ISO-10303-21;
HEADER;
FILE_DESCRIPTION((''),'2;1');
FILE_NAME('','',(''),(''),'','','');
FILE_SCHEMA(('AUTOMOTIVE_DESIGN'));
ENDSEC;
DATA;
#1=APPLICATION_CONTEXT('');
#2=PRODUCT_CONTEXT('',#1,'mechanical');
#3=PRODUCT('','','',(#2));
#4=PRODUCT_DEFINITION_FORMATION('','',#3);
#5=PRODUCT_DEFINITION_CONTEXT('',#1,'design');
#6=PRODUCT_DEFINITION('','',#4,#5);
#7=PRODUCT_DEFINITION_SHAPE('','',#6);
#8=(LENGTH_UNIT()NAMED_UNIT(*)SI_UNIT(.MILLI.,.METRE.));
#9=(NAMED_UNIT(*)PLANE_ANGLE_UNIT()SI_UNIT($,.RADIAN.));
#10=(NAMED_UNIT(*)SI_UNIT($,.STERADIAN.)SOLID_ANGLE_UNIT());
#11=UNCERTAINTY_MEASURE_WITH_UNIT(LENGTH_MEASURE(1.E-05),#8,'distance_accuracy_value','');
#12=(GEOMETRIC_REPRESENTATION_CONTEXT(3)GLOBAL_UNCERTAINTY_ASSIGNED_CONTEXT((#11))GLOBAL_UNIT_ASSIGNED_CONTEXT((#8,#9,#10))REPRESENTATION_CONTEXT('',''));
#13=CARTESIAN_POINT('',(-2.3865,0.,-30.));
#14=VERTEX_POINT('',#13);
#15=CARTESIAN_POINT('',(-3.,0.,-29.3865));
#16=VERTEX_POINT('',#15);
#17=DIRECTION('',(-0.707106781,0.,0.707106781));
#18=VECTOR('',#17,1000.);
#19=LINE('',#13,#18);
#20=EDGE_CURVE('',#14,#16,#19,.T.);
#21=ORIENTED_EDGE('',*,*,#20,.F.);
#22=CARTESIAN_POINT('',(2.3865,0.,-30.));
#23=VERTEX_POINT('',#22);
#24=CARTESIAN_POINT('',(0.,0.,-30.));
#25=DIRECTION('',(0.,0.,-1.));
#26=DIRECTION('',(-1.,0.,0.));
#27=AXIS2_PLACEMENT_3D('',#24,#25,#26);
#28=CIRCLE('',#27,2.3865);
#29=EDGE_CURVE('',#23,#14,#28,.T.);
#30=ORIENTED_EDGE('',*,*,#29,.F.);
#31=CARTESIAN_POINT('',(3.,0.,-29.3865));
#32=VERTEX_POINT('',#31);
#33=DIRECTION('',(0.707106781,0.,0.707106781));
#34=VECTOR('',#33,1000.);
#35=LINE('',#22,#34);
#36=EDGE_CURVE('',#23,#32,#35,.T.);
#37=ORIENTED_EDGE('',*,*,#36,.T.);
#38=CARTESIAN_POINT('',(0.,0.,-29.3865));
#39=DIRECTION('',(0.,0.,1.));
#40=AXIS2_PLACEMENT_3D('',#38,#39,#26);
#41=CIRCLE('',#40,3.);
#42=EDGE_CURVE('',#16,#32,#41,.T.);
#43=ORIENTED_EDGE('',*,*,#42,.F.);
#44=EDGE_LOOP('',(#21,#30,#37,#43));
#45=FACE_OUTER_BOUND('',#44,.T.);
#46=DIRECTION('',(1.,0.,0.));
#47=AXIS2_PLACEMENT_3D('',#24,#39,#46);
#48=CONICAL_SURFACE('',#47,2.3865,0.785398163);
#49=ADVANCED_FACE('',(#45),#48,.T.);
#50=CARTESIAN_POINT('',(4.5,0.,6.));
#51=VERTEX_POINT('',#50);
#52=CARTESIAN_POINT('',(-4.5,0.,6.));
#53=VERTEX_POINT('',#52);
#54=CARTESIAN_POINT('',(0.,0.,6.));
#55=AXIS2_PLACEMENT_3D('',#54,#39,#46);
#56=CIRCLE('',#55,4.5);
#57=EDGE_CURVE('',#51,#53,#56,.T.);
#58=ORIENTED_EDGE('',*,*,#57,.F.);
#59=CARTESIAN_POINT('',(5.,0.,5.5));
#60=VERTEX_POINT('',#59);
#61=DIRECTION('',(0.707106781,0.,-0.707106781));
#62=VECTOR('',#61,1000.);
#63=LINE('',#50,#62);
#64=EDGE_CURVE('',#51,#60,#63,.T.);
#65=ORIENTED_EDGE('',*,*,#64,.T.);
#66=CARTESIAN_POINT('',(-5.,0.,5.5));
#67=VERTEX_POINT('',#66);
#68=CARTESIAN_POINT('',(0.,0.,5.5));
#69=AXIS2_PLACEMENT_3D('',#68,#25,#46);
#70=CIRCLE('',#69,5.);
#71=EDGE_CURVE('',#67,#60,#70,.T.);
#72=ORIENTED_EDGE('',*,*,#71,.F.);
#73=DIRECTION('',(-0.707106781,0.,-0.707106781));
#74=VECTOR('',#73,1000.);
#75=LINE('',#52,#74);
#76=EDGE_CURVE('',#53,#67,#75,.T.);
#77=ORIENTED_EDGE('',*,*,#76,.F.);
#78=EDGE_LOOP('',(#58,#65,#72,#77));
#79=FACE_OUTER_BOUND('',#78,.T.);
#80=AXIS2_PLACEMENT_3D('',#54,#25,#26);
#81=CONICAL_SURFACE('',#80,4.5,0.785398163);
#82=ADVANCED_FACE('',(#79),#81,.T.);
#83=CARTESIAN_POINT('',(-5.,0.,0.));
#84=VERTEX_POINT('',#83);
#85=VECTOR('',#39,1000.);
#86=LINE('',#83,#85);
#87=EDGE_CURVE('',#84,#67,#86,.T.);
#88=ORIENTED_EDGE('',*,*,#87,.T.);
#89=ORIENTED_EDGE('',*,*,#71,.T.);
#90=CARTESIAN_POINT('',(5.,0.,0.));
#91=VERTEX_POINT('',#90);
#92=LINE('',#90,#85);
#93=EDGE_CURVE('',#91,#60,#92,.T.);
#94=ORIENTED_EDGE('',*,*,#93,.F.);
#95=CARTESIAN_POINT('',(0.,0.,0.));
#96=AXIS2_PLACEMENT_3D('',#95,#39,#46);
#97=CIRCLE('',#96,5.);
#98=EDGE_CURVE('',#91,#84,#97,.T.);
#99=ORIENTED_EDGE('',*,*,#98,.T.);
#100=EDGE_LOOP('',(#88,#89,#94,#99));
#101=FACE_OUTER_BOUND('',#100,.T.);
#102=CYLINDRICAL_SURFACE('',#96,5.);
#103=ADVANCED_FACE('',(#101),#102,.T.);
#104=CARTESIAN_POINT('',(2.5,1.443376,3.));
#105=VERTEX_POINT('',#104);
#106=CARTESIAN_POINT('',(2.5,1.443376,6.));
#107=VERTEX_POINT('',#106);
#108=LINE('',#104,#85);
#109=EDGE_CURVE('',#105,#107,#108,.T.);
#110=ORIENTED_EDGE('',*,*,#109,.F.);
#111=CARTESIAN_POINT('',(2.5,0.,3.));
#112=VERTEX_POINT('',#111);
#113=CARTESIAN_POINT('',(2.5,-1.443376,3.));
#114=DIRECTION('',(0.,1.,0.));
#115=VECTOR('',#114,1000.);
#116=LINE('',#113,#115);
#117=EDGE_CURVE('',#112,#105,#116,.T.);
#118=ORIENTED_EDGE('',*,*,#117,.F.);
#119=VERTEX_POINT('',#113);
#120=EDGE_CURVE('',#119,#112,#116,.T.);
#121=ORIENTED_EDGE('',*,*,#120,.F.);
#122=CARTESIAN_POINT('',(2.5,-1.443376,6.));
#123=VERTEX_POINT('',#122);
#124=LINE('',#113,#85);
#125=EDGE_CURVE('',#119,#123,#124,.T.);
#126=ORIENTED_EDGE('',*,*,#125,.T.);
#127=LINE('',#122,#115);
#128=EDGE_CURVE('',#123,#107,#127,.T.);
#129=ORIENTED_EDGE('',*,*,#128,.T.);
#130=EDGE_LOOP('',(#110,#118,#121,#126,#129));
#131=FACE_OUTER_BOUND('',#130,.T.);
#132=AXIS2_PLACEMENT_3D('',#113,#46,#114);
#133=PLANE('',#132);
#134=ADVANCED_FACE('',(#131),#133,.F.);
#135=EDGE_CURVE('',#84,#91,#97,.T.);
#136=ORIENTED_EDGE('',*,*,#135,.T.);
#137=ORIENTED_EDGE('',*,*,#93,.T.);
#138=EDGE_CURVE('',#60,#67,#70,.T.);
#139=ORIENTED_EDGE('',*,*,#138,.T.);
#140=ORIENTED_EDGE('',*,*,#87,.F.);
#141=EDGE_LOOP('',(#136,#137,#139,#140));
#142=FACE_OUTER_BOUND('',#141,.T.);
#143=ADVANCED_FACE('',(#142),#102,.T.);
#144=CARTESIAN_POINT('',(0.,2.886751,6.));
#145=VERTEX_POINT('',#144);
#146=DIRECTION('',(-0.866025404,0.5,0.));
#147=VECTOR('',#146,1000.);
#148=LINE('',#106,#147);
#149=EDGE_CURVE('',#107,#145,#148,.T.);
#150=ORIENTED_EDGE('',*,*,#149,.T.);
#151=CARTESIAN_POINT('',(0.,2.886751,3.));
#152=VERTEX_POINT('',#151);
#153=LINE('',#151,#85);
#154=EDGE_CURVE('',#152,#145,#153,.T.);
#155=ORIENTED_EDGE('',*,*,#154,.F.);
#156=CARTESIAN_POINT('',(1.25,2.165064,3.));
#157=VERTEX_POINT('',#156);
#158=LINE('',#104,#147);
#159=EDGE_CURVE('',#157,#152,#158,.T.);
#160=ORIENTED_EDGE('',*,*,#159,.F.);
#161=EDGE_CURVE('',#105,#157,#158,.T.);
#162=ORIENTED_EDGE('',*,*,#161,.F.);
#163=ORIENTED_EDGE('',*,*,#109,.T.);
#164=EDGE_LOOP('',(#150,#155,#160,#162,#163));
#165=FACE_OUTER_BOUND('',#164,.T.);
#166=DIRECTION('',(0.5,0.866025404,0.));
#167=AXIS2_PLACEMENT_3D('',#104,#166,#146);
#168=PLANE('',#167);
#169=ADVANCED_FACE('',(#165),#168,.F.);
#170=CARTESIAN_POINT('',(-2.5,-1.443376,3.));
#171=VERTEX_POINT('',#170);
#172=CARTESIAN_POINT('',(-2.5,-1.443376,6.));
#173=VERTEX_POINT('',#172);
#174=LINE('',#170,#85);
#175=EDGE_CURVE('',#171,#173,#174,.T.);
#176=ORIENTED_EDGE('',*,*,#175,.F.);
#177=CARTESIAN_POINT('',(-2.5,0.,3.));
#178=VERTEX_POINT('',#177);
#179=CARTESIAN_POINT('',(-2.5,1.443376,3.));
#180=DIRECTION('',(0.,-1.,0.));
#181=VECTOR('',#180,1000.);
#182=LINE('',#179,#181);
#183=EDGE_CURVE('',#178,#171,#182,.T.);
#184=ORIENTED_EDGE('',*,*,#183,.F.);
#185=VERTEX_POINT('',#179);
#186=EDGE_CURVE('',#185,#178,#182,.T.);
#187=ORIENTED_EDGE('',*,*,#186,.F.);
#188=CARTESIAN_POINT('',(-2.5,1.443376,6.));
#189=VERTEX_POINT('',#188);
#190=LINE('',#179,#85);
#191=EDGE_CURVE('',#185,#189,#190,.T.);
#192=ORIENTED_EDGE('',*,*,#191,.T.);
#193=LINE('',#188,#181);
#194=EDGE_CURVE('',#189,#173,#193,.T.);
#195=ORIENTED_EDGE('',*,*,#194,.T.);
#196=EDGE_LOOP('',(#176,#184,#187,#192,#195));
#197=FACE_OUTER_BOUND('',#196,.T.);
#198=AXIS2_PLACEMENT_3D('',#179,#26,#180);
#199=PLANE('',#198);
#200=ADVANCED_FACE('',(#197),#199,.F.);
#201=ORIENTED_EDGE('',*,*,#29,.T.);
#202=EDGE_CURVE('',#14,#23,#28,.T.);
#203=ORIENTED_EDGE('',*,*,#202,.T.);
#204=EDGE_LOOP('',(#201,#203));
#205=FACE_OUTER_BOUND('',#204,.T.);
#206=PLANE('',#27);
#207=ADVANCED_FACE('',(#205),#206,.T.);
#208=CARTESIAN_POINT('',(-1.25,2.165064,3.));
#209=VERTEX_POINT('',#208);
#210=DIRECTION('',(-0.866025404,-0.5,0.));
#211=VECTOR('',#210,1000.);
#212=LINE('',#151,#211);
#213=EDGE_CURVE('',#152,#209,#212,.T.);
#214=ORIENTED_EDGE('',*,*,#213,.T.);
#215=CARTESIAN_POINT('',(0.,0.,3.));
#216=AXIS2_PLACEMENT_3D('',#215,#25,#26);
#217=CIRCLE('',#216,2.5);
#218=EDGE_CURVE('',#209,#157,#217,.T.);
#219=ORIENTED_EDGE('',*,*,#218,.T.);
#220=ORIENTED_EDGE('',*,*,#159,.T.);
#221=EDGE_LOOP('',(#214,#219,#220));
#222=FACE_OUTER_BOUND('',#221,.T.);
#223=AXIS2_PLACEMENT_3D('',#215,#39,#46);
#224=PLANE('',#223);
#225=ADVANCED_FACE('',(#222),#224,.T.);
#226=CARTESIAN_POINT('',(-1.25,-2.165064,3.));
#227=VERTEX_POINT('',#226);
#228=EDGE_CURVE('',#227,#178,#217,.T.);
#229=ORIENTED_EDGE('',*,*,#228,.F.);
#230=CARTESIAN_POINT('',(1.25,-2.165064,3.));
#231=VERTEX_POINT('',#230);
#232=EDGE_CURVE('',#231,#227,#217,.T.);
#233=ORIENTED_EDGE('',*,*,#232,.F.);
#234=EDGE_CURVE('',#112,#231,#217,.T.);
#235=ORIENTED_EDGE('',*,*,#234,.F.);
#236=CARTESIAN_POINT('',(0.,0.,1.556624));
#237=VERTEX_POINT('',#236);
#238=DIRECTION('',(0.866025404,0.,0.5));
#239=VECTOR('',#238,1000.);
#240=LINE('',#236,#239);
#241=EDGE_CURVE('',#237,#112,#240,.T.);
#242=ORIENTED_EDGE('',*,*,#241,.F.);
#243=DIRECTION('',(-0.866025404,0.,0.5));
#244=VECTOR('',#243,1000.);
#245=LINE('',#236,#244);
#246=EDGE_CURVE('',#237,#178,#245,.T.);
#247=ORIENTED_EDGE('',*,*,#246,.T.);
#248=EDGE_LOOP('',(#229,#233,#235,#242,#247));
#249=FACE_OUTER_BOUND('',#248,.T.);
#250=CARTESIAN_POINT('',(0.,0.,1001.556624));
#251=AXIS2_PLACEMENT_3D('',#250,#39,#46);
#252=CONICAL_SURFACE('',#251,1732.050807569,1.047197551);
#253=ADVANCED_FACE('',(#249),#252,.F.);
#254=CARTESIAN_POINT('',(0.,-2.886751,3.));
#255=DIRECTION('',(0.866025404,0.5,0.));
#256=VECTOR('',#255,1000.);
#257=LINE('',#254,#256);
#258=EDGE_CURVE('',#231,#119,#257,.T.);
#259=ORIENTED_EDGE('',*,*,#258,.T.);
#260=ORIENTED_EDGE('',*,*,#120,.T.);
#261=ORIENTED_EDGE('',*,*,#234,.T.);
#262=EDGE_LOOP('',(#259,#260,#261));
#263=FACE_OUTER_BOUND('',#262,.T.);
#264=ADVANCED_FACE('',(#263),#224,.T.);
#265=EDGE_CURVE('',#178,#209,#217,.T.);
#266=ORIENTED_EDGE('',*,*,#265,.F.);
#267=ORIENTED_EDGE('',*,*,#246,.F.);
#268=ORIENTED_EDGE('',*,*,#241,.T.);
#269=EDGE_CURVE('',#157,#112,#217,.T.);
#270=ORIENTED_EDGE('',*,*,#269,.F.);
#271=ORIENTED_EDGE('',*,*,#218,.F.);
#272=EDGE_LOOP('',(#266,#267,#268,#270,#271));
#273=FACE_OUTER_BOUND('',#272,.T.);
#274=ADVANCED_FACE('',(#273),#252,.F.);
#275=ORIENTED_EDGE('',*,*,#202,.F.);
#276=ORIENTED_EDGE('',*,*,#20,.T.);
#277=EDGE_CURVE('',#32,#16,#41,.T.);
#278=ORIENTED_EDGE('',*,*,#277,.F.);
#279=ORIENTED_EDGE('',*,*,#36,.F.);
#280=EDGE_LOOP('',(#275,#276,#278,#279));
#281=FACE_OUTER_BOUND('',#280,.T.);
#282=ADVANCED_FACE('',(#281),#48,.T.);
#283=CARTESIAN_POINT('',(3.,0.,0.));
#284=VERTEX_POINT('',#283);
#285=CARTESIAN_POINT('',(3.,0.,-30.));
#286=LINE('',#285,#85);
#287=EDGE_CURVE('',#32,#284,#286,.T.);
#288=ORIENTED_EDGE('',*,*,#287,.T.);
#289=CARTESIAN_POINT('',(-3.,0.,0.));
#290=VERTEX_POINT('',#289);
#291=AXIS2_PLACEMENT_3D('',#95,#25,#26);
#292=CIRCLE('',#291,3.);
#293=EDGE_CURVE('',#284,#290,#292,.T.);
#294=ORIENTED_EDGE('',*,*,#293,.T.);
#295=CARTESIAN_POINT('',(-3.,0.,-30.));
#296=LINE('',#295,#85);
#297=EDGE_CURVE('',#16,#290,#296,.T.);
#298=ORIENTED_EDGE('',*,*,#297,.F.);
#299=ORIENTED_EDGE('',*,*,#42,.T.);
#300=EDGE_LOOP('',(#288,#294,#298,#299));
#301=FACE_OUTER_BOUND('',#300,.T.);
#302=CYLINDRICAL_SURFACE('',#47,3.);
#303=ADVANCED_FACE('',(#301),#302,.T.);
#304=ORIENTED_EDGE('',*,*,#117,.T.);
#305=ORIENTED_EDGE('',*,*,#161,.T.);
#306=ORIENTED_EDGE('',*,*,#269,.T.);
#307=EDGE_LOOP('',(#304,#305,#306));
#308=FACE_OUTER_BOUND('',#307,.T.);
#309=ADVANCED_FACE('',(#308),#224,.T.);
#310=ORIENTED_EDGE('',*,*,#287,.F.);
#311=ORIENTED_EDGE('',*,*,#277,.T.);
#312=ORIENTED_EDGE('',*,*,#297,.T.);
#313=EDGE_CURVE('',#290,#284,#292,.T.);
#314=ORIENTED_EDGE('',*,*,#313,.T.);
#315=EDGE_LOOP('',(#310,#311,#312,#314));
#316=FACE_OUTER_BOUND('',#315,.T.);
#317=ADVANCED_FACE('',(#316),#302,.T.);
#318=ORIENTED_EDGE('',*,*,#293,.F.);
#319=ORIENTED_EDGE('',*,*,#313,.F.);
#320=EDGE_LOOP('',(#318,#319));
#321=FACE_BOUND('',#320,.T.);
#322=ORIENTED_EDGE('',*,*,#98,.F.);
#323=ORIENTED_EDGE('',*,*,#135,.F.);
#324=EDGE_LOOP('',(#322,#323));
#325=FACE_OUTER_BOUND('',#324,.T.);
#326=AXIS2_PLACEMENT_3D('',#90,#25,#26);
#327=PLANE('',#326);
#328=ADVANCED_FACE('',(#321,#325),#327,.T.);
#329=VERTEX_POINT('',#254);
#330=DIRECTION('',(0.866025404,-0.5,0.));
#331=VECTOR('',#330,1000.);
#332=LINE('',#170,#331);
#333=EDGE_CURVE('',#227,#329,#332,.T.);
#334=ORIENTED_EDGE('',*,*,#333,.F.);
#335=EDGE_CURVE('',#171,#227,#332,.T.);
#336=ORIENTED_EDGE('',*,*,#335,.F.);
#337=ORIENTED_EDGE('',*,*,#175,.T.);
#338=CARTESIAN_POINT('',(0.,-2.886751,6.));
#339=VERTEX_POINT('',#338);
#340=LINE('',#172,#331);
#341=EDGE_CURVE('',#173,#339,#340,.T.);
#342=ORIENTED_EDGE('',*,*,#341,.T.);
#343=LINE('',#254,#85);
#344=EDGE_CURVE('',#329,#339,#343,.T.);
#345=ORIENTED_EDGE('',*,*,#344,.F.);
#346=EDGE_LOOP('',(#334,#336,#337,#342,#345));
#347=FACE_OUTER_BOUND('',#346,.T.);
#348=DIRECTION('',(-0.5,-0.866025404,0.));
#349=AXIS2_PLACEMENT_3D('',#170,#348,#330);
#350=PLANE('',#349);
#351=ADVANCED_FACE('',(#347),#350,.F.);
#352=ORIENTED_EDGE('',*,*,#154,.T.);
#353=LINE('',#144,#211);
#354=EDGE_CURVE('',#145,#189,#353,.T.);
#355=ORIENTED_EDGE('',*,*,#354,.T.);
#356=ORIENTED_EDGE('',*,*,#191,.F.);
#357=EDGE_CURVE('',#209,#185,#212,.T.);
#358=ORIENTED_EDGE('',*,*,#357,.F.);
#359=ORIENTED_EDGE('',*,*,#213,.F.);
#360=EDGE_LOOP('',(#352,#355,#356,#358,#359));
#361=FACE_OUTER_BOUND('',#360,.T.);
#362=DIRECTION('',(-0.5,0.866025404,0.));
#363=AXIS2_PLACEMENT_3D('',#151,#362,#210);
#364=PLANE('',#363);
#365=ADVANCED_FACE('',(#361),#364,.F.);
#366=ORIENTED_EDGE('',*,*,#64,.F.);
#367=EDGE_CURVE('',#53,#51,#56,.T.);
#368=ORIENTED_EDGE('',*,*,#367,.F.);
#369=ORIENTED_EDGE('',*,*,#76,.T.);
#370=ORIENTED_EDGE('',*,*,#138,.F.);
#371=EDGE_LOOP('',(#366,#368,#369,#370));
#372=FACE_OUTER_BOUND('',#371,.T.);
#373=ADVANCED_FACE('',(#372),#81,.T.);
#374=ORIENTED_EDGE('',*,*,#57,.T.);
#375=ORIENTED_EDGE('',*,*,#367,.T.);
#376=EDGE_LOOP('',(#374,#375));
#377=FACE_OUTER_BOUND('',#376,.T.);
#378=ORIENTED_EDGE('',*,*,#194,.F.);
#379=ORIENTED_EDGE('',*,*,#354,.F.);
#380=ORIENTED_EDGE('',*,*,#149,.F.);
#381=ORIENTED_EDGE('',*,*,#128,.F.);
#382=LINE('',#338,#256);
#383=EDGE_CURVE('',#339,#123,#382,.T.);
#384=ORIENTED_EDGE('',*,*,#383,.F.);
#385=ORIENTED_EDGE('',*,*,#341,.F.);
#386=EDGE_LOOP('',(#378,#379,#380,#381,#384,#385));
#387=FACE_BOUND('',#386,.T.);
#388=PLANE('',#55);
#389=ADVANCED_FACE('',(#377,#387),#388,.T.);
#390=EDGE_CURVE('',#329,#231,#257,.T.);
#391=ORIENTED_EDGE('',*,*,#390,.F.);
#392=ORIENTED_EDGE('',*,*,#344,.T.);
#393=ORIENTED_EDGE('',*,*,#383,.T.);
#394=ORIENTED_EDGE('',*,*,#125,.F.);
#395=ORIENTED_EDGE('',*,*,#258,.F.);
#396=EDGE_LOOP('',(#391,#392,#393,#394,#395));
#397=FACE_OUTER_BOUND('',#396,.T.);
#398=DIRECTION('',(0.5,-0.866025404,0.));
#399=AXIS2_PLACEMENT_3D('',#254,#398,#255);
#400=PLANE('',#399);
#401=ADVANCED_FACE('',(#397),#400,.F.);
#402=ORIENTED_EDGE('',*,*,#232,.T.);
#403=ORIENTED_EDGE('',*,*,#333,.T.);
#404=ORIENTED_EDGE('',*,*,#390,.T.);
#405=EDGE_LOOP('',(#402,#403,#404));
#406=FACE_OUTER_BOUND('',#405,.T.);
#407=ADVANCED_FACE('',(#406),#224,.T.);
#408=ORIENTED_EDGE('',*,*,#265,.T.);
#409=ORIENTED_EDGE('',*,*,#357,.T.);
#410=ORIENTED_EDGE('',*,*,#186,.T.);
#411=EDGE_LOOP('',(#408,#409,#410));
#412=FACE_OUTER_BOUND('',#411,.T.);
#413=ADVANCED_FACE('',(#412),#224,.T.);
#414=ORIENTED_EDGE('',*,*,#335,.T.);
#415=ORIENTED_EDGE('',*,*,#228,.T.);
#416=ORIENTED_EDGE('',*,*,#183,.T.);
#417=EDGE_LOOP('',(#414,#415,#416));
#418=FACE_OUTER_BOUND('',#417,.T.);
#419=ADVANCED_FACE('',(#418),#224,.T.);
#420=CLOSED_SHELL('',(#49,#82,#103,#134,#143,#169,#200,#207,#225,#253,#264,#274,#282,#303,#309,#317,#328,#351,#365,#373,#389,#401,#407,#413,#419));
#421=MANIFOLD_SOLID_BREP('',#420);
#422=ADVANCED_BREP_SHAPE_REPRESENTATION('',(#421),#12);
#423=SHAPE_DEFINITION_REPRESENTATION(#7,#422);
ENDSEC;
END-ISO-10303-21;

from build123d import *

# Parameters (mm, degrees)
SKETCH_1_W          = 5
SKETCH_1_H          = 6
SKETCH_2_R          = 3
EXTRUDE_1_DEPTH     = 30
CUT_EXTRUDE_1_DEPTH = 3
CHAMFER_1_SIZE      = 0.5
CHAMFER_2_SIZE      = 0.6135


with BuildPart() as part:
    # 草图1 → 旋转1 (revolve)
    with BuildSketch(Plane(origin=(0, 0, 0), x_dir=(1, 0, 0), z_dir=(0, 1, 0))):
        with Locations((2.5, -3)):
            Rectangle(SKETCH_1_W, SKETCH_1_H)
    revolve(axis=Axis((0, 0, 0), (0, 0, 1)))

    # 草图2 → 凸台-拉伸1 (add)
    with BuildSketch(Plane(origin=(0, 0, 0), x_dir=(-1, 0, 0), z_dir=(0, 0, -1))):
        Circle(SKETCH_2_R)
    extrude(amount=EXTRUDE_1_DEPTH)

    # 草图3 → 切除-拉伸1 (cut)
    with BuildSketch(Plane.XY.offset(6)):
        Polygon((2.5, 1.443375673), (0, 2.886751346), (-2.5, 1.443375673), (-2.5, -1.443375673), (0, -2.886751346), (2.5, -1.443375673), align=None)
    extrude(amount=-CUT_EXTRUDE_1_DEPTH, mode=Mode.SUBTRACT)

    # 草图4 → 切除-旋转1 (revolve, cut)
    with BuildSketch(Plane.XZ):
        Polygon((2.5, 3), (0, 3), (0, 1.556624327), align=None)
    revolve(axis=Axis((0, 0, 3), (0, 0, -1)), mode=Mode.SUBTRACT)

    # 倒角1
    chamfer_1_edges = [part.edges().sort_by_distance(p)[0] for p in [
        (-5, 0, 6),
    ]]
    chamfer(chamfer_1_edges, length=CHAMFER_1_SIZE)

    # 倒角2
    chamfer_2_edges = [part.edges().sort_by_distance(p)[0] for p in [
        (3, 0, -30),
    ]]
    chamfer(chamfer_2_edges, length=CHAMFER_2_SIZE)


solid = part.part
